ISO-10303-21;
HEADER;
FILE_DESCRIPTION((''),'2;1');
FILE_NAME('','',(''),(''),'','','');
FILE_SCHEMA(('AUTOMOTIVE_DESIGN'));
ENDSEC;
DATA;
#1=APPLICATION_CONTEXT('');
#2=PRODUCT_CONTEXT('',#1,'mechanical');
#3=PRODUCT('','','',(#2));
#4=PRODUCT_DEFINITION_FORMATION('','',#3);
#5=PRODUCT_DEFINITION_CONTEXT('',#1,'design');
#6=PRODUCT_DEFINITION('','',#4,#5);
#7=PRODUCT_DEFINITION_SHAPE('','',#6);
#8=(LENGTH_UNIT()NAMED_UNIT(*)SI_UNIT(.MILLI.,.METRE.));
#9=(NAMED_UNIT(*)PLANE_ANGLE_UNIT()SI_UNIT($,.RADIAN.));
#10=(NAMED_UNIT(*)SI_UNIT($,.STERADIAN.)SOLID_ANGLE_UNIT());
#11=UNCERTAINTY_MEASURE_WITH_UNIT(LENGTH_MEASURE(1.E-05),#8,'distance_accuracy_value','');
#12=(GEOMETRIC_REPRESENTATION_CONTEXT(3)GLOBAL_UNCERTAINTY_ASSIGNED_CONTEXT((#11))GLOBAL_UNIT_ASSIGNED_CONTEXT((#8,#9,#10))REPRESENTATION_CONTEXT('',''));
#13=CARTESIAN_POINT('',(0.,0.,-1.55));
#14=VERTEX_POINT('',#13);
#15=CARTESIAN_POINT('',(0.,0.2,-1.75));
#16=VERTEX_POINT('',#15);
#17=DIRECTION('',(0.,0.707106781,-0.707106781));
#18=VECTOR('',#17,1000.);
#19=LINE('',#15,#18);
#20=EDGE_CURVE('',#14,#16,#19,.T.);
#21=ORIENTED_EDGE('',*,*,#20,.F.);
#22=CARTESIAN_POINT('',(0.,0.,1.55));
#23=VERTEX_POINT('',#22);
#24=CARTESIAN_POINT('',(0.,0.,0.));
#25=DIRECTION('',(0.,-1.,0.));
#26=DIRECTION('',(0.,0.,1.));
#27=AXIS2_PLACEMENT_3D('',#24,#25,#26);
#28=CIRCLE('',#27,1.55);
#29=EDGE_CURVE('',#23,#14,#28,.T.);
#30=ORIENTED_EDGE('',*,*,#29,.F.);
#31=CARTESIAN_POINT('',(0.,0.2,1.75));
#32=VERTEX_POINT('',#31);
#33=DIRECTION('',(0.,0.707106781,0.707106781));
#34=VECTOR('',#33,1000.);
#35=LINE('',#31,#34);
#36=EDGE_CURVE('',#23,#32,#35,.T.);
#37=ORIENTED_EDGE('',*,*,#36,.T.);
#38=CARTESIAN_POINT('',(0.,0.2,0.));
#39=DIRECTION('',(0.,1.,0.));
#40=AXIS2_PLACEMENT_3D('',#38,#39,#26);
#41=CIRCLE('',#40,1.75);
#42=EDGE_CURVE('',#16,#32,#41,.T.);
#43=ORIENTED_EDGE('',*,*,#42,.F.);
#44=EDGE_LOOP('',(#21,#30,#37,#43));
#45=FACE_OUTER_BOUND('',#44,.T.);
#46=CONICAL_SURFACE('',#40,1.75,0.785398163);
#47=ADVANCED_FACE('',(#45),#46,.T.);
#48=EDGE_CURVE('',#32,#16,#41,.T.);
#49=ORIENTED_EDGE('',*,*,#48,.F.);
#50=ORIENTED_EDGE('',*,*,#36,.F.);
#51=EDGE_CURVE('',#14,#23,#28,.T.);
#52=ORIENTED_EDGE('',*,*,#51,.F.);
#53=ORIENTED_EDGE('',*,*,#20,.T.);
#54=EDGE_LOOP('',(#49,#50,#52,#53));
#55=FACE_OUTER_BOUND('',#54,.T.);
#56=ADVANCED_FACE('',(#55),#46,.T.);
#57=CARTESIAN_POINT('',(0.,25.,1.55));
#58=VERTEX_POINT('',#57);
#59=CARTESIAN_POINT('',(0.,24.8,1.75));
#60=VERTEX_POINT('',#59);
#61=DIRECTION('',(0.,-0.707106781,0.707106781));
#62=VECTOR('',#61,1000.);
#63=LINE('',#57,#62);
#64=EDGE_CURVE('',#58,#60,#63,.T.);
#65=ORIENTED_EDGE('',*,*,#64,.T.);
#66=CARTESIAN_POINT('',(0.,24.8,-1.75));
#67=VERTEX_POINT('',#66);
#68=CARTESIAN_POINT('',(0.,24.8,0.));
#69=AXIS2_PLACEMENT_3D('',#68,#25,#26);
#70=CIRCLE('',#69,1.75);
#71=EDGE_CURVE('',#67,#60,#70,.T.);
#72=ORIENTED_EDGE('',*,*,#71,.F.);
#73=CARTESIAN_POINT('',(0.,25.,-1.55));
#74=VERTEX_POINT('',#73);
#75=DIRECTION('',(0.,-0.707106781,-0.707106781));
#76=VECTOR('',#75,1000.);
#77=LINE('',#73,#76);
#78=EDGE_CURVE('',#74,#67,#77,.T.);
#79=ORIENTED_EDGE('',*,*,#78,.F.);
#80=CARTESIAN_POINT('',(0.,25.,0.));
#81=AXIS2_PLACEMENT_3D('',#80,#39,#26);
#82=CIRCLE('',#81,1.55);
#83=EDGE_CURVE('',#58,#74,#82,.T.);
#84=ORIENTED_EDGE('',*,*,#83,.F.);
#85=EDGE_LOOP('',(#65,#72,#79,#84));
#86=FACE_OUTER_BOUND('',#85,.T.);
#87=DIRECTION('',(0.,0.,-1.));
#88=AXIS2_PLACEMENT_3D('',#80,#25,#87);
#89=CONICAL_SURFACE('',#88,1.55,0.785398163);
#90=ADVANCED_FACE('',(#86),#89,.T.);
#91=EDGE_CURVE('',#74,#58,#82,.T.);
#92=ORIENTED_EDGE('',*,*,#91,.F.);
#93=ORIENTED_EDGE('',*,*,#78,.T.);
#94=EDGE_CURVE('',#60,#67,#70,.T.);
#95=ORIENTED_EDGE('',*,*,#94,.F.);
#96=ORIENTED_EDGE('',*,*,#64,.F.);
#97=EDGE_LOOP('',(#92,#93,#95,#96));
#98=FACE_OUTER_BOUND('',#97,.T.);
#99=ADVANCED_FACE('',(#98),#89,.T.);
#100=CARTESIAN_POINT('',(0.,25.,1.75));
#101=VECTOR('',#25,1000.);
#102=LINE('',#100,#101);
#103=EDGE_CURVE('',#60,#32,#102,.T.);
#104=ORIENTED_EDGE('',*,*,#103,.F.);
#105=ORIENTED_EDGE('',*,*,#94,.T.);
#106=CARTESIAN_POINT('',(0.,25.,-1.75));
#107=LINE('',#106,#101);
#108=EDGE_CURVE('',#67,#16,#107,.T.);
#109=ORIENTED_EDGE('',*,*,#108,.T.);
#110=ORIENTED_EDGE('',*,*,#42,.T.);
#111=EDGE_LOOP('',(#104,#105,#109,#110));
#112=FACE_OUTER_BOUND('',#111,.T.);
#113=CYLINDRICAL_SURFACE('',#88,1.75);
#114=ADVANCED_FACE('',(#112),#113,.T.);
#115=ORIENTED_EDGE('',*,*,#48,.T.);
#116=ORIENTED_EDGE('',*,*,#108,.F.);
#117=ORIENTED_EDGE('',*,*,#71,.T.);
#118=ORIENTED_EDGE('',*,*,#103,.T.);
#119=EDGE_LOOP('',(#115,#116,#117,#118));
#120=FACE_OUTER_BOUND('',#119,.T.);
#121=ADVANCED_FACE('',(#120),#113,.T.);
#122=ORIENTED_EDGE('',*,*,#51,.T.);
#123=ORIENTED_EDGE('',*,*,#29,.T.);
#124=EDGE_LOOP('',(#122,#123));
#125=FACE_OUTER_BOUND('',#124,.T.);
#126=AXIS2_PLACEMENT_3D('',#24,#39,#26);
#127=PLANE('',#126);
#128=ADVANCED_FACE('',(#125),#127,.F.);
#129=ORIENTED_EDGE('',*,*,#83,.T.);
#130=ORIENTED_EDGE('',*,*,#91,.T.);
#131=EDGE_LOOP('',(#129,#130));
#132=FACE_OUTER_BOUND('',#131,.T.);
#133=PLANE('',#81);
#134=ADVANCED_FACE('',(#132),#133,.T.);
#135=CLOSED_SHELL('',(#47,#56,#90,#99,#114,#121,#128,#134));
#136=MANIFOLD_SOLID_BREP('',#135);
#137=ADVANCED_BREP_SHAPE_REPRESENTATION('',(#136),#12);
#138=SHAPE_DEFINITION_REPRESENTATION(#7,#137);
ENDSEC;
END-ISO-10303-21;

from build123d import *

# Parameters (mm, degrees)
SKETCH_1_R      = 1.75
EXTRUDE_1_DEPTH = 25
CHAMFER_1_SIZE  = 0.2


with BuildPart() as part:
    # 草图1 → 凸台-拉伸1 (new body)
    with BuildSketch(Plane(origin=(0, 0, 0), x_dir=(1, 0, 0), z_dir=(0, 1, 0))):
        with Locations(Location((0, 0, 0), (0, 0, 270))):
            Circle(SKETCH_1_R)
    extrude(amount=EXTRUDE_1_DEPTH)

    # 倒角1
    chamfer_1_edges = [part.edges().sort_by_distance(p)[0] for p in [
        (0, 0, -1.75),
        (0, 25, -1.75),
    ]]
    chamfer(chamfer_1_edges, length=CHAMFER_1_SIZE)


solid = part.part
